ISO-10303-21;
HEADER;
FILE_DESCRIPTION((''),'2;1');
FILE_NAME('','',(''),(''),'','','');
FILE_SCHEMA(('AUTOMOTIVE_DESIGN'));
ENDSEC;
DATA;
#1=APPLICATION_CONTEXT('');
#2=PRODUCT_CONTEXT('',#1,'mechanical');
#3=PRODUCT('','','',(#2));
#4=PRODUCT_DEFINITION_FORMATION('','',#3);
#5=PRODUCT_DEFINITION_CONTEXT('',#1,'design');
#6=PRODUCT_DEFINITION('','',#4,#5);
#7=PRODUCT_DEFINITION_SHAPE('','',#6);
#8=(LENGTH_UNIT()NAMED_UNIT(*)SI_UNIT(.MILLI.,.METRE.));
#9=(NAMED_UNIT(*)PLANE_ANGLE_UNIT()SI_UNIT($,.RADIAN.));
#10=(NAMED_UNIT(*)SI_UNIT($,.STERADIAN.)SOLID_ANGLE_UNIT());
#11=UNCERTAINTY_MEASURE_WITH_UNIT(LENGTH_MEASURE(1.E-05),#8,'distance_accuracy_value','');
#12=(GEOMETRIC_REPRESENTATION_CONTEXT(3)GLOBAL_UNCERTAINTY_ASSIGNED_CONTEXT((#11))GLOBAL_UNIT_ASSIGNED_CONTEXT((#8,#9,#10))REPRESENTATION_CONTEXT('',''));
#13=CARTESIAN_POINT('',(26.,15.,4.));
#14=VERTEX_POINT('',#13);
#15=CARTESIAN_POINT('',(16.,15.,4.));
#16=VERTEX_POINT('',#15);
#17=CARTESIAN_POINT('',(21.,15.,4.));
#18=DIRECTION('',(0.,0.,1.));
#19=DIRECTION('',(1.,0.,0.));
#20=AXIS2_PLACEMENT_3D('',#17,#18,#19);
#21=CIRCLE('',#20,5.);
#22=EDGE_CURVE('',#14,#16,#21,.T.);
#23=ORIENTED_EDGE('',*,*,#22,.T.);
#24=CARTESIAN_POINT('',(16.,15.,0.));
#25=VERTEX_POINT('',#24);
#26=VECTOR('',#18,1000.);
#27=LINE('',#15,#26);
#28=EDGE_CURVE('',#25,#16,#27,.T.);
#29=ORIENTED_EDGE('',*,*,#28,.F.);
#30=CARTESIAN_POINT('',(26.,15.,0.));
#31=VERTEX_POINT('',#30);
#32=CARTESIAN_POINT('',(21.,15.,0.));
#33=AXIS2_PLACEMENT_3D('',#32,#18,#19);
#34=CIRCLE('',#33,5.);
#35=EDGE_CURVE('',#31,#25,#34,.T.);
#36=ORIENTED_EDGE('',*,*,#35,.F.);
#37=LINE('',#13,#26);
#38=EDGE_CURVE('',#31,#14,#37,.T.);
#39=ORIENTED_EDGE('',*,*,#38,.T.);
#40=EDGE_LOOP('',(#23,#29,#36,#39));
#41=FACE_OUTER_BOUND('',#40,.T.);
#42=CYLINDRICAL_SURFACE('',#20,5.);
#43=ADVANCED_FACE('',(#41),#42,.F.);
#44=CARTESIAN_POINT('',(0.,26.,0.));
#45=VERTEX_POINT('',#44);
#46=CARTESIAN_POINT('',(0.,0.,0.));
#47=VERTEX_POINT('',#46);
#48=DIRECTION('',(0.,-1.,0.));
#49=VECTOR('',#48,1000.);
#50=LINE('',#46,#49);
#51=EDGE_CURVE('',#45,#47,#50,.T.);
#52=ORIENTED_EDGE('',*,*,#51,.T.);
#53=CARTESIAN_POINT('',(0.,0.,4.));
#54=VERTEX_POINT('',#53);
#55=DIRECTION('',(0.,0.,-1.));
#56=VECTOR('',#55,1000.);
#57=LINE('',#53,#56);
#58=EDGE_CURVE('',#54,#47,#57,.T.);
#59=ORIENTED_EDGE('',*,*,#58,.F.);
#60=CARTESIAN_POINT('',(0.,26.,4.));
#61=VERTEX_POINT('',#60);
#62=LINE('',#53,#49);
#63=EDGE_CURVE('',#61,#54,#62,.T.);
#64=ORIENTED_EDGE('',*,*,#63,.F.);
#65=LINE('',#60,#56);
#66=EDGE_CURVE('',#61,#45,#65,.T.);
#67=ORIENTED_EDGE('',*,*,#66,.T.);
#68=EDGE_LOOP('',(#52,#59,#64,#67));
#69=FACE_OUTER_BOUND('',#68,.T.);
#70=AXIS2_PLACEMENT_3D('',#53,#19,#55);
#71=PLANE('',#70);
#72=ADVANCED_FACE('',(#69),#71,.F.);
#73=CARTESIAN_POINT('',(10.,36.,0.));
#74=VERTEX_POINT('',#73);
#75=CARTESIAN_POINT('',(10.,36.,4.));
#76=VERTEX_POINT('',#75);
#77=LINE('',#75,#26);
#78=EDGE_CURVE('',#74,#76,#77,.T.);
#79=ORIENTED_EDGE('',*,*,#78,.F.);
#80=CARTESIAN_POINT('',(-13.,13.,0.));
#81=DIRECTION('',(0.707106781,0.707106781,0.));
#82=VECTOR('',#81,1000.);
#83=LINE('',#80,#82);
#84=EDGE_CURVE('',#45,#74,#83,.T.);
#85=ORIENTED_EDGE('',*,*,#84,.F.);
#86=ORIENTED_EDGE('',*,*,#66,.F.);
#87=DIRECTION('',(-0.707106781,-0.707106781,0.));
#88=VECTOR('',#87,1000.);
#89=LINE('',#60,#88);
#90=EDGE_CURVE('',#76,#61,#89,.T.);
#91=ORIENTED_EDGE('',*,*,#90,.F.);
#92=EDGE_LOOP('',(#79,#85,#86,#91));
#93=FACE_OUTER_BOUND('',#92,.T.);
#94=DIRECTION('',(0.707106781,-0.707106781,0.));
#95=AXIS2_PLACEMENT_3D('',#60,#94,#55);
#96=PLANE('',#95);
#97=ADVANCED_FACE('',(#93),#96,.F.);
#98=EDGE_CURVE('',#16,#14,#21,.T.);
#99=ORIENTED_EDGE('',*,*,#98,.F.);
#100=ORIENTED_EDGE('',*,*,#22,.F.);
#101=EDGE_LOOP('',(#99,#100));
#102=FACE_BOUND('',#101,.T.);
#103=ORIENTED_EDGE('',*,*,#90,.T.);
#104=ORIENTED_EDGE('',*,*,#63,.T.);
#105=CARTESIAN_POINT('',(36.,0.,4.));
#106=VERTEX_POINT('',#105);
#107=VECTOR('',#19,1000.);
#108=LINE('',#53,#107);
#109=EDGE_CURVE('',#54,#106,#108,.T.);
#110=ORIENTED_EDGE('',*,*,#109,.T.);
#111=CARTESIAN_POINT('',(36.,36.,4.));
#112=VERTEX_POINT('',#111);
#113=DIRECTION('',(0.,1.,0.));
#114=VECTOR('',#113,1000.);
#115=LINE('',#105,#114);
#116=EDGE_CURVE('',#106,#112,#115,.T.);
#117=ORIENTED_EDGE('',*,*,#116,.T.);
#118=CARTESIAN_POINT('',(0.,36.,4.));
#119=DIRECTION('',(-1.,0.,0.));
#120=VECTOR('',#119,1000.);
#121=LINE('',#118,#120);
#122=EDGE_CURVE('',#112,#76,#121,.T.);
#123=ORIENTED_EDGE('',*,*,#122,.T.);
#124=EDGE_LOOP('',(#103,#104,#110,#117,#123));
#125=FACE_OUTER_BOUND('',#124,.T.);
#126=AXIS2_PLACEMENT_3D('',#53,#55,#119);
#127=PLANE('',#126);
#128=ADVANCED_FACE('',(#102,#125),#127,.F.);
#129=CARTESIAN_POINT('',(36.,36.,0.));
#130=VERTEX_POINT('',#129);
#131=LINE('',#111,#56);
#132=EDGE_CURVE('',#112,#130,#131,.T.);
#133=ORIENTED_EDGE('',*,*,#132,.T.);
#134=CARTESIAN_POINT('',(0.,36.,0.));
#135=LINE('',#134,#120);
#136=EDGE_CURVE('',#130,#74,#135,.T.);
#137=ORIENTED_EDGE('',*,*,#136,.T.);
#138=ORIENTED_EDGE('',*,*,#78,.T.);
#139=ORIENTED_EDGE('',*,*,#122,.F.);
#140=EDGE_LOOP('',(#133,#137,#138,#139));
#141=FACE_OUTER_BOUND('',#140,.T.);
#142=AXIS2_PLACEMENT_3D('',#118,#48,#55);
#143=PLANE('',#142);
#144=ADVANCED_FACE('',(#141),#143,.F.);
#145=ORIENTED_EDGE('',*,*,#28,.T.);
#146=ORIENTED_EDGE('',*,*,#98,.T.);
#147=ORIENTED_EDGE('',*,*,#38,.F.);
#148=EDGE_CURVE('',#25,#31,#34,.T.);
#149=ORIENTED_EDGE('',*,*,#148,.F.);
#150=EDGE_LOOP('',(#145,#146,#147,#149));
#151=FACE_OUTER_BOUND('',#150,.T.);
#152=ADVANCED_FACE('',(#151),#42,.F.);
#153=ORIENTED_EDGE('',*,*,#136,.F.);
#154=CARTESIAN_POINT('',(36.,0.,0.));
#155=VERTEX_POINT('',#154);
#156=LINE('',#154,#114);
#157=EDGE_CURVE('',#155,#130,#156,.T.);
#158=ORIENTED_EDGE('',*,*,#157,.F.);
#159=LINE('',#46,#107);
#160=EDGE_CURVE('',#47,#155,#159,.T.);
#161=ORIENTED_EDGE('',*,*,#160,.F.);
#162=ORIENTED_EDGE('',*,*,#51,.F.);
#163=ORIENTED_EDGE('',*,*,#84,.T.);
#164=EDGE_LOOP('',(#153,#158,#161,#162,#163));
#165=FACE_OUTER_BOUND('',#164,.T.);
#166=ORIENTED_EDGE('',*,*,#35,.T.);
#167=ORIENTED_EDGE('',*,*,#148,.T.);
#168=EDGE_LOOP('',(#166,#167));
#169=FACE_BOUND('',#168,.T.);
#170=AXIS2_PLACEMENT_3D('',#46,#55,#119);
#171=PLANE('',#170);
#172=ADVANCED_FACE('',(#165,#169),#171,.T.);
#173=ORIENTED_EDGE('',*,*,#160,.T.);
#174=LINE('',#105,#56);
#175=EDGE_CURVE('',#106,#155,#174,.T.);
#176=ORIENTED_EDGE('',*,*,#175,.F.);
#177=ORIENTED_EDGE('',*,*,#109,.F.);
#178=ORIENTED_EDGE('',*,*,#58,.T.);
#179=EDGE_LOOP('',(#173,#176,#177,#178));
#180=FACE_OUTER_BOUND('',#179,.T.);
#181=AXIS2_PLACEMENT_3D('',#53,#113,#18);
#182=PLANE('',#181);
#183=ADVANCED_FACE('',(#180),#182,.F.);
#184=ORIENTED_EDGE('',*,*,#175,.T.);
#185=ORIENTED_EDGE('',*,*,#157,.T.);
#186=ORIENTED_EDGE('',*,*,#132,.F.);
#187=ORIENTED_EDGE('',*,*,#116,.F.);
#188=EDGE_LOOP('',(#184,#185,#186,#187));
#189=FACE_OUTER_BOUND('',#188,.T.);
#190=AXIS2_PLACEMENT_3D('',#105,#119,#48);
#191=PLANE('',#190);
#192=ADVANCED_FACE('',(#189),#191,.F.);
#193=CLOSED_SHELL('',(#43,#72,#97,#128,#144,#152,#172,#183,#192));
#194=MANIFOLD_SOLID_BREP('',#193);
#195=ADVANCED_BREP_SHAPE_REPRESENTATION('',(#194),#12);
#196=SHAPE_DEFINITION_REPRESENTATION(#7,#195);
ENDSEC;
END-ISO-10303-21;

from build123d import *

# Parameters (mm, degrees)
SKETCH_1_W              = 36
SKETCH_1_H              = 36
EXTRUDE_1_DEPTH         = 4
CHAMFER_1_SIZE          = 10
HOLE_WIZARD_10_0_10_1_D = 10


with BuildPart() as part:
    # 草图1 → 凸台-拉伸1 (new body)
    with BuildSketch(Plane.XY):
        with Locations((18, 18)):
            Rectangle(SKETCH_1_W, SKETCH_1_H)
    extrude(amount=EXTRUDE_1_DEPTH)

    # 倒角1
    chamfer_1_edges = [part.edges().sort_by_distance(p)[0] for p in [
        (0, 36, 2),
    ]]
    chamfer(chamfer_1_edges, length=CHAMFER_1_SIZE)

    # Ø10.0 (10) 直径孔1 (through all)
    with Locations(Plane.XY.offset(4)):
        with Locations((21, 15)):
            Hole(HOLE_WIZARD_10_0_10_1_D / 2)


solid = part.part
